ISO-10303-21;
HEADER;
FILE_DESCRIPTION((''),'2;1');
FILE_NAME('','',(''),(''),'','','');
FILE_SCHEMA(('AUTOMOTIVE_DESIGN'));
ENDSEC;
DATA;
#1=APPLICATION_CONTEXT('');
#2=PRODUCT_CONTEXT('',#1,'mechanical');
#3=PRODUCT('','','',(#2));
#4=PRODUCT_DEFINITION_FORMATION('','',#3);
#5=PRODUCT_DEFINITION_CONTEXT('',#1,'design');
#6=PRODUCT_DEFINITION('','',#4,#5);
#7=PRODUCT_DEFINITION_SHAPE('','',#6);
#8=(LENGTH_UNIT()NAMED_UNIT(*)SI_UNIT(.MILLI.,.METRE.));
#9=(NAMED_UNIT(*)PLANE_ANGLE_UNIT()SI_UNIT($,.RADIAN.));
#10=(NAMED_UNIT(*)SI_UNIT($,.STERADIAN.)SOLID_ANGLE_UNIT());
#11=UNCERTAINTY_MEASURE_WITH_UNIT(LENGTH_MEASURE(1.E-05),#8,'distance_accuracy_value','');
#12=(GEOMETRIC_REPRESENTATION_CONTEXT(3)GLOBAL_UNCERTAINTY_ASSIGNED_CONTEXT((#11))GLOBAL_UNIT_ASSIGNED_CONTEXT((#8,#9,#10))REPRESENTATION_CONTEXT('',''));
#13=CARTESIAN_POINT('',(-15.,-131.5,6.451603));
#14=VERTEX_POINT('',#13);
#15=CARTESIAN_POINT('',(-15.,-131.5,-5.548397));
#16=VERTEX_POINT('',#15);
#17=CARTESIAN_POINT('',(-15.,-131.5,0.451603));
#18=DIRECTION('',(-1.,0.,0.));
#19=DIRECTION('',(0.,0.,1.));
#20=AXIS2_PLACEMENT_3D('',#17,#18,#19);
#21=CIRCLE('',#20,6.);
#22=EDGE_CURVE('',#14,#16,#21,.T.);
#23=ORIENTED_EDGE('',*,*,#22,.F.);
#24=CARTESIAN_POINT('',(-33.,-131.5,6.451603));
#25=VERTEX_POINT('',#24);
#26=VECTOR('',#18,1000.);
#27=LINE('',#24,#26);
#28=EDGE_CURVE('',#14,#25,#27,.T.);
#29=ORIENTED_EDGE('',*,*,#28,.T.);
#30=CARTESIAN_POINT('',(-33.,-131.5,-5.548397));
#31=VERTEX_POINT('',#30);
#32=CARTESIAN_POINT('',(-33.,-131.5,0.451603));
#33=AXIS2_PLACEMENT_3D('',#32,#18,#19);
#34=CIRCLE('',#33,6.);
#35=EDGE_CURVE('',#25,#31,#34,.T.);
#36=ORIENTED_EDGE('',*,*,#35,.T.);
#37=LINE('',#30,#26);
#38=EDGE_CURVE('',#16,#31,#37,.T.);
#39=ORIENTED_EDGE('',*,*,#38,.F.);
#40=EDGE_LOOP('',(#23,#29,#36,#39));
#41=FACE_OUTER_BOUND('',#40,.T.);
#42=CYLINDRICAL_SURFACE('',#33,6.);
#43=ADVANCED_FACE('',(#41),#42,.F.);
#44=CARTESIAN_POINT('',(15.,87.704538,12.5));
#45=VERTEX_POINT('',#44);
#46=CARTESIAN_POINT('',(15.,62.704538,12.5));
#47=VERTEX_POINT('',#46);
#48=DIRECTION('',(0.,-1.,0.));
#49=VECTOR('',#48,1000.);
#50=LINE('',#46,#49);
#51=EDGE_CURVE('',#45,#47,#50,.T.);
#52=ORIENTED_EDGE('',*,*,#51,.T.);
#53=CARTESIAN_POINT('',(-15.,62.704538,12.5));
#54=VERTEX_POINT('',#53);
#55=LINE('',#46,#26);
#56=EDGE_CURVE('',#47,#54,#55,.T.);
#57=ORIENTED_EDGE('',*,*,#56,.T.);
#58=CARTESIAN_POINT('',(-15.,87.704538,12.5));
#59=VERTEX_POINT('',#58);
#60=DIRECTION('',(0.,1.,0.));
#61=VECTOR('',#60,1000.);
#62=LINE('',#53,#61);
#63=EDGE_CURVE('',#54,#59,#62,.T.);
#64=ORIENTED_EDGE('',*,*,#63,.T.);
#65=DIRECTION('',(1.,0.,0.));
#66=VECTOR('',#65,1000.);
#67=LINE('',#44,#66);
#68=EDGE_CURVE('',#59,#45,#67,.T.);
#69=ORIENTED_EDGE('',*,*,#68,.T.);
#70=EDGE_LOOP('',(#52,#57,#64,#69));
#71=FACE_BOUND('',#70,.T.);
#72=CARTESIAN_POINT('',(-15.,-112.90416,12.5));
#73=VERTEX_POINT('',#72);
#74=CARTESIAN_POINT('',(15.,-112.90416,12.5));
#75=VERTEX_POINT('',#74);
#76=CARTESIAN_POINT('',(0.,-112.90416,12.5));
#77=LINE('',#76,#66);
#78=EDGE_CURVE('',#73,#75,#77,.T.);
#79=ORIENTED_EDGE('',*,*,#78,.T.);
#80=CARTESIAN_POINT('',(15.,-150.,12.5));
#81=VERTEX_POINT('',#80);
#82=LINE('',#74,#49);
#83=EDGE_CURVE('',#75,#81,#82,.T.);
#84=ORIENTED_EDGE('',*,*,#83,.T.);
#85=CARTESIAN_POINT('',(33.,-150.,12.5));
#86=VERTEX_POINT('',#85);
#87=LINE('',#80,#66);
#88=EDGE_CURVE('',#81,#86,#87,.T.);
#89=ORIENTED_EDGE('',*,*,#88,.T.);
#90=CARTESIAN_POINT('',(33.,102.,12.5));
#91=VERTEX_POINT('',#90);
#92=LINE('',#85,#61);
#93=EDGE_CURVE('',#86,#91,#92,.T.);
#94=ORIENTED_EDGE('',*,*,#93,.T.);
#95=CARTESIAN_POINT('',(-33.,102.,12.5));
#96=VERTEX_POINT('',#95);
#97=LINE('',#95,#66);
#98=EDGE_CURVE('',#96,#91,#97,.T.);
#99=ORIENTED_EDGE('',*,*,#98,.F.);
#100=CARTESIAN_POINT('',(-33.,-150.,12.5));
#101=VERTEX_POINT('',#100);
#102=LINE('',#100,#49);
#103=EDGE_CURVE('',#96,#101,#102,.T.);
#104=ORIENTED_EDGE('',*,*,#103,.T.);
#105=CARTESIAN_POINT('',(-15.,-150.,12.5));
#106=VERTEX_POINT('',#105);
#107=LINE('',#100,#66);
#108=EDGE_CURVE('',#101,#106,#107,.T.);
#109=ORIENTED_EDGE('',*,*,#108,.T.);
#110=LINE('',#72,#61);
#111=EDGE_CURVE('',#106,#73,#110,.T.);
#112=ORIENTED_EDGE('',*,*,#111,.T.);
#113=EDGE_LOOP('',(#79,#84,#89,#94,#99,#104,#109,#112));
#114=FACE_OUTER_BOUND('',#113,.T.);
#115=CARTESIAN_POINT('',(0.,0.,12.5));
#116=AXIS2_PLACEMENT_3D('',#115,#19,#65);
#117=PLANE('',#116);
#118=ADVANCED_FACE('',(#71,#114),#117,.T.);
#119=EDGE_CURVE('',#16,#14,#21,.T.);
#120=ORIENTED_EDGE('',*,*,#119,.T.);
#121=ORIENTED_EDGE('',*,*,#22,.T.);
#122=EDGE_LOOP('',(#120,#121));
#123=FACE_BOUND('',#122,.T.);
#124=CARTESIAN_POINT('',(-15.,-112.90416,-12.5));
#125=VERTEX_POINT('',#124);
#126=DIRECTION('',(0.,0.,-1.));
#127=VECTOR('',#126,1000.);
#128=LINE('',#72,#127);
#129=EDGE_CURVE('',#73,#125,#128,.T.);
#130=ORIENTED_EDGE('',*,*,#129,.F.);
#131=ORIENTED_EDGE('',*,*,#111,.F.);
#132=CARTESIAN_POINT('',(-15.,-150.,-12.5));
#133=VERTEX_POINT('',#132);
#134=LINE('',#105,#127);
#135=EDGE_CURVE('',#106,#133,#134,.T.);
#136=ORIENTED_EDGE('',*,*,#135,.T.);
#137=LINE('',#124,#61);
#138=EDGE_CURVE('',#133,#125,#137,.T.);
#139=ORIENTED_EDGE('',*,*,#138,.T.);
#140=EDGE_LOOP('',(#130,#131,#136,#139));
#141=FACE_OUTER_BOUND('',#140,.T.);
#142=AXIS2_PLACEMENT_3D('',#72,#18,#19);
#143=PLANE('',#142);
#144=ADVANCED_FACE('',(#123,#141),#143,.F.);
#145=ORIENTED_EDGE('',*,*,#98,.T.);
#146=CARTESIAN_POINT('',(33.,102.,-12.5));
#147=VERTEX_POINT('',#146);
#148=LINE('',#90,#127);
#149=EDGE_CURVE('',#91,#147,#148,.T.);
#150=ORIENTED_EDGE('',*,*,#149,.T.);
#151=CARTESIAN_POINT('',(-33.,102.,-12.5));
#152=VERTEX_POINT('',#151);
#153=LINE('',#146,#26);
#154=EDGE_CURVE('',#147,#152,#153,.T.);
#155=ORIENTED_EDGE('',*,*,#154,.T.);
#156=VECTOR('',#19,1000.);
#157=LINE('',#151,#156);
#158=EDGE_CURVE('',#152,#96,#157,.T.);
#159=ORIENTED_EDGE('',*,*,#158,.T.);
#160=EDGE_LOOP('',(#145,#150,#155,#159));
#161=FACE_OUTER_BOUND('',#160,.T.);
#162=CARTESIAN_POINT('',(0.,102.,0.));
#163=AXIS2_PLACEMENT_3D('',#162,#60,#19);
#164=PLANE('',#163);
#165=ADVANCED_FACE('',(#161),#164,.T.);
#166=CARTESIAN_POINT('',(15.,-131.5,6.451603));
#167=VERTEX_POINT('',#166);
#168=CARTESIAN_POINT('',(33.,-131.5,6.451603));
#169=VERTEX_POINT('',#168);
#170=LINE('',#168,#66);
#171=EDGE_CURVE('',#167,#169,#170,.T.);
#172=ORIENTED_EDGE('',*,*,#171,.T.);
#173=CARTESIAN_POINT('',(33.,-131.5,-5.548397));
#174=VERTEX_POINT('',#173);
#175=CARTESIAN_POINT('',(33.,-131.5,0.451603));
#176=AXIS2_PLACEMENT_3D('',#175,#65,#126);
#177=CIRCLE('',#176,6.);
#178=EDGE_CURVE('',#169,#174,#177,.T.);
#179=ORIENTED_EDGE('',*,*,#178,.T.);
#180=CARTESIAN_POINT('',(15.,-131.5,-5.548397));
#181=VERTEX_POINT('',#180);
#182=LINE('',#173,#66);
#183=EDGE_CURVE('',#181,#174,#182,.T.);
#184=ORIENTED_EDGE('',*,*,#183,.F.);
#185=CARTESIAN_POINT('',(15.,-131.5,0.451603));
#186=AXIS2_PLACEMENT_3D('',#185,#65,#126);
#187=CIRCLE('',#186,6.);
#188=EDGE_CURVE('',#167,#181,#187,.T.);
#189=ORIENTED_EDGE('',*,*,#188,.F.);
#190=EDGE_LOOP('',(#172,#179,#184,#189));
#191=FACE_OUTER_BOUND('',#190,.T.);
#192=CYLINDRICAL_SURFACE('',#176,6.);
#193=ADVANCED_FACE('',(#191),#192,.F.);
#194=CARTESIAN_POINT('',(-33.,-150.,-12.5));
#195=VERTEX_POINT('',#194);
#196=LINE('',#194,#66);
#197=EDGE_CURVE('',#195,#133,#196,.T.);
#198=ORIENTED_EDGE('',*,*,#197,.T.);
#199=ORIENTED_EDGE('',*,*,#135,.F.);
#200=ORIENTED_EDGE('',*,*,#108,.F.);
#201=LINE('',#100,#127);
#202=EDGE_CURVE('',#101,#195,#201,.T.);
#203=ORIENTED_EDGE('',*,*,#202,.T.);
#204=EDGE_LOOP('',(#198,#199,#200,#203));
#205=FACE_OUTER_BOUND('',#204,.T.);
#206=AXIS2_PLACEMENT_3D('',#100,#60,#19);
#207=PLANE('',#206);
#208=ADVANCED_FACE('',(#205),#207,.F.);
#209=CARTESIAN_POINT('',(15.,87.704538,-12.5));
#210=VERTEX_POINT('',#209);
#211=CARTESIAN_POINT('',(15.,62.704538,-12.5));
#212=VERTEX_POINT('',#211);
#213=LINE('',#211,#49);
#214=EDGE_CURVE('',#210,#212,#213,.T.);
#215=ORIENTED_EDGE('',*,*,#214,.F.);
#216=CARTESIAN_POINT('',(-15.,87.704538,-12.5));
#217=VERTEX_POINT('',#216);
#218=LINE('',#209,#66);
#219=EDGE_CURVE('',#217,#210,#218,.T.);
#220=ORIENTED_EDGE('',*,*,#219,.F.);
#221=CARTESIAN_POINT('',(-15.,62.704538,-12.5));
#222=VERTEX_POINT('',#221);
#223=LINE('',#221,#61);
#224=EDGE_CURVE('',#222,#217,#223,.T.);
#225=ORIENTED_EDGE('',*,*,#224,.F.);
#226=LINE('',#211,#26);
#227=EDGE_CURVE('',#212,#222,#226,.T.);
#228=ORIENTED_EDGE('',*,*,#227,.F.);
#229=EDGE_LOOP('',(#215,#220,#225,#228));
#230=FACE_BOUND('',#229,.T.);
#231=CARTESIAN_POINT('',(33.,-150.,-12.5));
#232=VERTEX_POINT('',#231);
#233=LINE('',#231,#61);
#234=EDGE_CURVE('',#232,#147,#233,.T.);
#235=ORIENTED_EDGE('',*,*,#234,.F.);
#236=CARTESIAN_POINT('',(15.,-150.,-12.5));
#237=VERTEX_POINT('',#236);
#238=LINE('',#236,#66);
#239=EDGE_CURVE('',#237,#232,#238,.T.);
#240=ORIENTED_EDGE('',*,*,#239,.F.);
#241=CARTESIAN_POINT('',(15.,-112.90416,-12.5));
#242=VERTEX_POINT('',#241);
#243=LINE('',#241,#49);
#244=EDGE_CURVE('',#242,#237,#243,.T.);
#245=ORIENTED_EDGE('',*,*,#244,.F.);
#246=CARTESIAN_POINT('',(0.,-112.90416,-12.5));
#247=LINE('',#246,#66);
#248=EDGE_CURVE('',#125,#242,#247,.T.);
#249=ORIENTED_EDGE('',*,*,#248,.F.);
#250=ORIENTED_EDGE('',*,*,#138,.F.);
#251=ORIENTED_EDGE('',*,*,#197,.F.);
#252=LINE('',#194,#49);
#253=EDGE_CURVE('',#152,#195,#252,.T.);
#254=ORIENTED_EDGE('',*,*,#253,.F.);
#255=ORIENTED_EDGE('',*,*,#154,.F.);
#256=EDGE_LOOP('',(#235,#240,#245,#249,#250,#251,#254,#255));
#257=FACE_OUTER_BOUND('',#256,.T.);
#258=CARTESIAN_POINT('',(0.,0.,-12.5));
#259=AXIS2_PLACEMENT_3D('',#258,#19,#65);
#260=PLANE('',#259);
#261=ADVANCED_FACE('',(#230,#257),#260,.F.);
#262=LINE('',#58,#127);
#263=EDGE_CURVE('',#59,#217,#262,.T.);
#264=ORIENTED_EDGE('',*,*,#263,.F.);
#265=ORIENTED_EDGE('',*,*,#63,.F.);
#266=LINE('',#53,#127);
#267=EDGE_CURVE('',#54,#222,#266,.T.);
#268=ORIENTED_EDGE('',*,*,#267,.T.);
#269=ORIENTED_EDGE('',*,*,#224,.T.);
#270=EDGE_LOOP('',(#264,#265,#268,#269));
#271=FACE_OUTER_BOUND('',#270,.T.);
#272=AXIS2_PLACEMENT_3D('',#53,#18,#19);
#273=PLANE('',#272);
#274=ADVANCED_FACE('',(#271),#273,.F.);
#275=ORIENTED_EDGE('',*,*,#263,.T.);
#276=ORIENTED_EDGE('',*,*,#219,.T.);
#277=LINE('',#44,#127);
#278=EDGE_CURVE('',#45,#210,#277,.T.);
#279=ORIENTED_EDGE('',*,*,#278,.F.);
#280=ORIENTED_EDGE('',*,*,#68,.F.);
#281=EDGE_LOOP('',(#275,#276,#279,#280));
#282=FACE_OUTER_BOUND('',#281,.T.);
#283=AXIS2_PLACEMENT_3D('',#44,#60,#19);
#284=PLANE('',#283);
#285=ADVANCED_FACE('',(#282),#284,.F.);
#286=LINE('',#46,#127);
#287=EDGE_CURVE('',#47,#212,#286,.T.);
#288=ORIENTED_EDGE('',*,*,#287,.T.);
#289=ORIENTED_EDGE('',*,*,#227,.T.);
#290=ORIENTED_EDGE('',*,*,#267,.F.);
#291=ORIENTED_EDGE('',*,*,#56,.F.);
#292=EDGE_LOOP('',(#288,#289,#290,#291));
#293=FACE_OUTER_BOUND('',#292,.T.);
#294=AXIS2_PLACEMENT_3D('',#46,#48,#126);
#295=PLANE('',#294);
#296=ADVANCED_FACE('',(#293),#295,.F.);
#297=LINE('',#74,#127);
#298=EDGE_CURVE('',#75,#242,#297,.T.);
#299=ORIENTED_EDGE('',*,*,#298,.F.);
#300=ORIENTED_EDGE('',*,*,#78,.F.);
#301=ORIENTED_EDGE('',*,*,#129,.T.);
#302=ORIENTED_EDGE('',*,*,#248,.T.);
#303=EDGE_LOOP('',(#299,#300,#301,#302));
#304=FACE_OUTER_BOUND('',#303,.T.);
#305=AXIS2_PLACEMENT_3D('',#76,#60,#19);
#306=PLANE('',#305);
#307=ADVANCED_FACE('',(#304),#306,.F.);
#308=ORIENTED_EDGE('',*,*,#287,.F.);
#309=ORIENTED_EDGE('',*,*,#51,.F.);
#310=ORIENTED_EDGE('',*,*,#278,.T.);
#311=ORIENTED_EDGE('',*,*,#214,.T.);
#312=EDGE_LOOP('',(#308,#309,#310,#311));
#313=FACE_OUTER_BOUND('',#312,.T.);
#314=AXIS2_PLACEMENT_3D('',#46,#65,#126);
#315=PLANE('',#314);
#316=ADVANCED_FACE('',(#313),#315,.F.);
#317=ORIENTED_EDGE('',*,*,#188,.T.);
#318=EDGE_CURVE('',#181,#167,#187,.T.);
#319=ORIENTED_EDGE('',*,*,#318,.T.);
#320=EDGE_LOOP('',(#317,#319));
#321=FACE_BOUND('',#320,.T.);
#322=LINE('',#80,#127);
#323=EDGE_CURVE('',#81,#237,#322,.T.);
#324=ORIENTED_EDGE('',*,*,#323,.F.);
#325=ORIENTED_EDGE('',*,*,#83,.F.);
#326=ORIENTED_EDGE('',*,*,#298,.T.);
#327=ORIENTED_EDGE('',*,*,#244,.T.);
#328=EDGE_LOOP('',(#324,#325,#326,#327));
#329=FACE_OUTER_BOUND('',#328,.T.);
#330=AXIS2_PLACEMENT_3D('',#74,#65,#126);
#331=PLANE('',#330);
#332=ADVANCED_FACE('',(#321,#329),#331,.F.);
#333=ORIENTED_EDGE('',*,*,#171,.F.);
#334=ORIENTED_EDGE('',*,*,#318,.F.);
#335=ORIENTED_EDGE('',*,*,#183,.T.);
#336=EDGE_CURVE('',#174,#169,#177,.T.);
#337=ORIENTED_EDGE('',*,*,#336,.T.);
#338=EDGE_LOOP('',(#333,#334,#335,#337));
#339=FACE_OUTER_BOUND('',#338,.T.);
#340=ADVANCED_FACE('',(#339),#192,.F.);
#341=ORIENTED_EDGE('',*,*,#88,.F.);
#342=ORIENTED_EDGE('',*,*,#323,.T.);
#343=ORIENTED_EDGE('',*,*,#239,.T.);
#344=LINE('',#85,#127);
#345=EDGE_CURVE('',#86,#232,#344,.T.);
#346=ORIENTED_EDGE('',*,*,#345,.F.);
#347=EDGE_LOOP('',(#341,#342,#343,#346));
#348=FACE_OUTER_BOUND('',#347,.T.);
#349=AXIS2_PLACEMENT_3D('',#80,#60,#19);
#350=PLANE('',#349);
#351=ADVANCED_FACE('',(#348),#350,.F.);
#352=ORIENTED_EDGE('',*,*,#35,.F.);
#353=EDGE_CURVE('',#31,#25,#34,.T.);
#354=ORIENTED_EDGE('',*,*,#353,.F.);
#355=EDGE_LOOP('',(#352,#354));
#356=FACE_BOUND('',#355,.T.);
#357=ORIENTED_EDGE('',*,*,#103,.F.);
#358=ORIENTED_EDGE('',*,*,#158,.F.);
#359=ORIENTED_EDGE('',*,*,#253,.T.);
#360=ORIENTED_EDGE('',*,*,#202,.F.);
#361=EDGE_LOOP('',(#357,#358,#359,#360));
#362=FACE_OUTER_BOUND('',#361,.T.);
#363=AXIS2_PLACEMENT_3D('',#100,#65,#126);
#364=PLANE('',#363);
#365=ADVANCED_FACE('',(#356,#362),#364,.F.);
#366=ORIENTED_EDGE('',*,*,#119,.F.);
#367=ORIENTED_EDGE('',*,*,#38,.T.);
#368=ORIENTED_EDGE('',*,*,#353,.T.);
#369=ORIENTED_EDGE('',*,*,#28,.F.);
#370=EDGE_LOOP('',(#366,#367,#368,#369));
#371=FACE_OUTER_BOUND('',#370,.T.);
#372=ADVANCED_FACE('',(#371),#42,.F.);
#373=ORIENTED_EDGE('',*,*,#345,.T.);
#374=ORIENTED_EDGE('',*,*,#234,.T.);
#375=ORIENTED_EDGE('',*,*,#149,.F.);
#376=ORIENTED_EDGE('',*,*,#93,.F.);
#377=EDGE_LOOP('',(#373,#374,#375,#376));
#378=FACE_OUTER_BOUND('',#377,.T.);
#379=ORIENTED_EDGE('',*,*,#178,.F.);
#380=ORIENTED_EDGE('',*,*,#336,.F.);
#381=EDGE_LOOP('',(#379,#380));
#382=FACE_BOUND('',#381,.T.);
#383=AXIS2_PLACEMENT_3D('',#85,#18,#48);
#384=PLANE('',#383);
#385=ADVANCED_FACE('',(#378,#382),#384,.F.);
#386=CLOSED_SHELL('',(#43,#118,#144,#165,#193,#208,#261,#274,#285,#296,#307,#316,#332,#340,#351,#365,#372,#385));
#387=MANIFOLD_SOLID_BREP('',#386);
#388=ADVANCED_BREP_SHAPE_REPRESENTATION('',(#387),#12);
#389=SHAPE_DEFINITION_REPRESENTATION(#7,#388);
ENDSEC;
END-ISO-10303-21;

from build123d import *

# Parameters (mm, degrees)
EXTRUDE_1_DEPTH          = 12.5
HOLE_WIZARD_M14_1_D      = 12
HOLE_WIZARD_M14_1_DEPTH  = 18
SKETCH_7_W               = 66
SKETCH_7_H               = 25
EXTRUDE_2_DEPTH          = 12
CUT_EXTRUDE_5_DEPTH      = 156.608483059
CUT_EXTRUDE_5_DEPTH_BACK = 156.608483059
SKETCH_12_W              = 30
SKETCH_12_H              = 25


with BuildPart() as part:
    # 草图1 → 凸台-拉伸1 (new, symmetric)
    with BuildSketch(Plane.XY):
        Polygon((-33, -150), (-15, -150), (-15, -112.904160338), (0, -112.904160338), (15, -112.904160338), (15, -150), (33, -150), (33, 90), (15, 90), (-15, 90), (-33, 90), align=None)
    extrude(amount=EXTRUDE_1_DEPTH, both=True)

    # M14 螺纹孔1
    with Locations(Plane(origin=(33, -131.5, 0.451602972), x_dir=(0, 0, 1), z_dir=(1, 0, 0))):
        with Locations((0, 0)):
            hole_wizard_m14_1 = Hole(HOLE_WIZARD_M14_1_D / 2, depth=HOLE_WIZARD_M14_1_DEPTH)

    # 镜向1: M14 螺纹孔1 across plane
    add(hole_wizard_m14_1.mirror(Plane(origin=(0, 0, 0), x_dir=(0, 0, 1), z_dir=(1, 0, 0))), mode=Mode.SUBTRACT)

    # 草图7 → 凸台-拉伸2 (add)
    with BuildSketch(Plane(origin=(0, 90, 0), x_dir=(1, 0, 0), z_dir=(0, 1, 0))):
        Rectangle(SKETCH_7_W, SKETCH_7_H)
    extrude(amount=EXTRUDE_2_DEPTH)

    # 草图12 → 切除-拉伸5 (cut, two sides: drawn at the far end of the back side and taken through both)
    with BuildSketch(Plane(origin=(0, 0, -12.5), x_dir=(-1, 0, 0), z_dir=(0, 0, -1)).offset(-CUT_EXTRUDE_5_DEPTH_BACK)):
        with Locations((0, 75.204537633)):
            Rectangle(SKETCH_12_W, SKETCH_12_H)
    extrude(amount=CUT_EXTRUDE_5_DEPTH + CUT_EXTRUDE_5_DEPTH_BACK, mode=Mode.SUBTRACT)


solid = part.part
